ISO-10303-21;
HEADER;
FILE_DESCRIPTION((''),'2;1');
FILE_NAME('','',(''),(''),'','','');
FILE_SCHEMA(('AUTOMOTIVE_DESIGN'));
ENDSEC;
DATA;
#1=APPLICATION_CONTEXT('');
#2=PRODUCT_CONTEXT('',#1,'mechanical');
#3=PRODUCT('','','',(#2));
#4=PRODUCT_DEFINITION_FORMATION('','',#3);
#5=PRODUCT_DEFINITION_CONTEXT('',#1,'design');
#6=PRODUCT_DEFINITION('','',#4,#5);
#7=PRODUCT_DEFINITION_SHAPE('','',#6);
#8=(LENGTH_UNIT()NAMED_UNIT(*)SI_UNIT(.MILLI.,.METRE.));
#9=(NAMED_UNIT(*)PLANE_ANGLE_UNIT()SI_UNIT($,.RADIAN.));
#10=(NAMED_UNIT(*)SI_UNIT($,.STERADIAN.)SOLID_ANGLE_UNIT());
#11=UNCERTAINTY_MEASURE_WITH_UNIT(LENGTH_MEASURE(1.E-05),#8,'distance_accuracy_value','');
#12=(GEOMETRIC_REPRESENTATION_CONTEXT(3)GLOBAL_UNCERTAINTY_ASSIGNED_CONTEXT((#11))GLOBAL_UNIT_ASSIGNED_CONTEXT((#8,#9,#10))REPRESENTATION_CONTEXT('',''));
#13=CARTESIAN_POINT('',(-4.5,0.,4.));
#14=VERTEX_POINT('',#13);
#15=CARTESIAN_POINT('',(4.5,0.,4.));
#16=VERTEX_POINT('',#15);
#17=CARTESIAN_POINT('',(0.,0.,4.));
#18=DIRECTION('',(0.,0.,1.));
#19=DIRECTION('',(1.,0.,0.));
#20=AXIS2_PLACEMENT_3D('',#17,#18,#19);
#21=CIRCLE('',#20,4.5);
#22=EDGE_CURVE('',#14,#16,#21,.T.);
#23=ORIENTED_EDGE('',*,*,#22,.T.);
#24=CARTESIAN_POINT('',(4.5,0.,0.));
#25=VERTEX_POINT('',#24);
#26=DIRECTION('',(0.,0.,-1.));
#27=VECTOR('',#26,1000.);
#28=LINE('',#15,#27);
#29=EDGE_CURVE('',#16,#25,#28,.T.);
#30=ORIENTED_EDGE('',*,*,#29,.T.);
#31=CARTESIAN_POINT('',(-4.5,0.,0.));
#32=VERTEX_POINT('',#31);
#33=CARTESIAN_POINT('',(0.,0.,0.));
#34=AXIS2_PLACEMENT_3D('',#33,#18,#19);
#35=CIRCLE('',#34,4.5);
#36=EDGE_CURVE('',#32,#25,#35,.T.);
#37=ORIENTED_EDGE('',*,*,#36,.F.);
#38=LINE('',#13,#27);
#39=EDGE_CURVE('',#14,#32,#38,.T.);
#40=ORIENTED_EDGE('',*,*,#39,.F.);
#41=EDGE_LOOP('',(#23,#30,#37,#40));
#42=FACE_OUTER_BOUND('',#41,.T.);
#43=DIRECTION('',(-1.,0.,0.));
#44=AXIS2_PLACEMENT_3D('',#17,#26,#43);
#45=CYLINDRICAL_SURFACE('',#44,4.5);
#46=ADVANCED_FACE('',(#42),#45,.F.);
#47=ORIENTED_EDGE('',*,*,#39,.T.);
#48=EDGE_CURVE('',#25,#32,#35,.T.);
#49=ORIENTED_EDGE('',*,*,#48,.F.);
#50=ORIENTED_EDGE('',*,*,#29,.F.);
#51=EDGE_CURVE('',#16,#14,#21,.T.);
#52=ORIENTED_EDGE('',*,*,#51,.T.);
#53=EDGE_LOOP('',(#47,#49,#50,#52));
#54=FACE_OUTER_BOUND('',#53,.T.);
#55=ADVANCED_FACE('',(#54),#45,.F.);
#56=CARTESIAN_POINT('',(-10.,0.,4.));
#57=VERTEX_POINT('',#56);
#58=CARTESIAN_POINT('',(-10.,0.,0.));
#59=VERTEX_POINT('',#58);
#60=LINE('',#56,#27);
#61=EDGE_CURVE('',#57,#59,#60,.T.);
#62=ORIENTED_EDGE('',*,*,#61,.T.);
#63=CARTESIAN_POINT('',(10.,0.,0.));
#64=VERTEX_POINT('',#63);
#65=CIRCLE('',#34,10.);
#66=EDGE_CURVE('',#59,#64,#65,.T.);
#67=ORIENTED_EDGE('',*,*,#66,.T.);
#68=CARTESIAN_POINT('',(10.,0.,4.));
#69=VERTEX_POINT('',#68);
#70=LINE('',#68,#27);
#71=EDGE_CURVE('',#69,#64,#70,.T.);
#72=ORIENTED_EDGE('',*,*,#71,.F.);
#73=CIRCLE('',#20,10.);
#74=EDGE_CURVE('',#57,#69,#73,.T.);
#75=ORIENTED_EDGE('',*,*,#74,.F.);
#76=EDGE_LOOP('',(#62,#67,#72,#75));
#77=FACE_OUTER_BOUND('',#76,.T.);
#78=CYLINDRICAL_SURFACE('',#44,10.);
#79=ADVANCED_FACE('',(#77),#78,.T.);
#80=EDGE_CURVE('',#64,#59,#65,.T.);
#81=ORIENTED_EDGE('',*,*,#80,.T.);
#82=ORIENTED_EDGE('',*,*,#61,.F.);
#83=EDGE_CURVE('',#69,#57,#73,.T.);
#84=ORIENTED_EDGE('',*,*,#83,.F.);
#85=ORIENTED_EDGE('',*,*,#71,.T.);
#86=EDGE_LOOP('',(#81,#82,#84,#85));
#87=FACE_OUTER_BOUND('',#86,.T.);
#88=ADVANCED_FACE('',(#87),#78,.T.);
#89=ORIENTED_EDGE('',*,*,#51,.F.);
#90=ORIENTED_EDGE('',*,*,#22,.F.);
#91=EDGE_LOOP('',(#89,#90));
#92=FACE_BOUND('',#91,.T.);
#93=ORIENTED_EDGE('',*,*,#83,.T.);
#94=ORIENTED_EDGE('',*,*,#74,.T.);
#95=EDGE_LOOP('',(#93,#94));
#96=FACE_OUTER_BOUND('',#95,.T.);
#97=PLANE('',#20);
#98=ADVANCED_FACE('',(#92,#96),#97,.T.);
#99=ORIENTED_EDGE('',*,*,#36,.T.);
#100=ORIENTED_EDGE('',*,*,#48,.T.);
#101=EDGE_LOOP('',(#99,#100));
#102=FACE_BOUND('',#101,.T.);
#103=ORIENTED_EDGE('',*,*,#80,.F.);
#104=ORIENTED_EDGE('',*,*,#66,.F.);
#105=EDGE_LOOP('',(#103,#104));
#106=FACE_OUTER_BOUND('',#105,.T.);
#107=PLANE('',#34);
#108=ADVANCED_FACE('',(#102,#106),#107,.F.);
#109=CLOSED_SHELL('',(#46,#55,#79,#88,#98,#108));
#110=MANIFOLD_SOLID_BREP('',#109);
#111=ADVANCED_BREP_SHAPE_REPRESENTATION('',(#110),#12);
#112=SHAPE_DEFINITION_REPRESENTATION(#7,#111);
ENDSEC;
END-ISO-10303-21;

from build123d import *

# Parameters (mm, degrees)
SKETCH_1_R      = 10
SKETCH_1_R_2    = 4.5
EXTRUDE_1_DEPTH = 4


with BuildPart() as part:
    # 草图1 → 凸台-拉伸1 (new body)
    with BuildSketch(Plane.XY):
        Circle(SKETCH_1_R)
        Circle(SKETCH_1_R_2, mode=Mode.SUBTRACT)
    extrude(amount=EXTRUDE_1_DEPTH)


solid = part.part
